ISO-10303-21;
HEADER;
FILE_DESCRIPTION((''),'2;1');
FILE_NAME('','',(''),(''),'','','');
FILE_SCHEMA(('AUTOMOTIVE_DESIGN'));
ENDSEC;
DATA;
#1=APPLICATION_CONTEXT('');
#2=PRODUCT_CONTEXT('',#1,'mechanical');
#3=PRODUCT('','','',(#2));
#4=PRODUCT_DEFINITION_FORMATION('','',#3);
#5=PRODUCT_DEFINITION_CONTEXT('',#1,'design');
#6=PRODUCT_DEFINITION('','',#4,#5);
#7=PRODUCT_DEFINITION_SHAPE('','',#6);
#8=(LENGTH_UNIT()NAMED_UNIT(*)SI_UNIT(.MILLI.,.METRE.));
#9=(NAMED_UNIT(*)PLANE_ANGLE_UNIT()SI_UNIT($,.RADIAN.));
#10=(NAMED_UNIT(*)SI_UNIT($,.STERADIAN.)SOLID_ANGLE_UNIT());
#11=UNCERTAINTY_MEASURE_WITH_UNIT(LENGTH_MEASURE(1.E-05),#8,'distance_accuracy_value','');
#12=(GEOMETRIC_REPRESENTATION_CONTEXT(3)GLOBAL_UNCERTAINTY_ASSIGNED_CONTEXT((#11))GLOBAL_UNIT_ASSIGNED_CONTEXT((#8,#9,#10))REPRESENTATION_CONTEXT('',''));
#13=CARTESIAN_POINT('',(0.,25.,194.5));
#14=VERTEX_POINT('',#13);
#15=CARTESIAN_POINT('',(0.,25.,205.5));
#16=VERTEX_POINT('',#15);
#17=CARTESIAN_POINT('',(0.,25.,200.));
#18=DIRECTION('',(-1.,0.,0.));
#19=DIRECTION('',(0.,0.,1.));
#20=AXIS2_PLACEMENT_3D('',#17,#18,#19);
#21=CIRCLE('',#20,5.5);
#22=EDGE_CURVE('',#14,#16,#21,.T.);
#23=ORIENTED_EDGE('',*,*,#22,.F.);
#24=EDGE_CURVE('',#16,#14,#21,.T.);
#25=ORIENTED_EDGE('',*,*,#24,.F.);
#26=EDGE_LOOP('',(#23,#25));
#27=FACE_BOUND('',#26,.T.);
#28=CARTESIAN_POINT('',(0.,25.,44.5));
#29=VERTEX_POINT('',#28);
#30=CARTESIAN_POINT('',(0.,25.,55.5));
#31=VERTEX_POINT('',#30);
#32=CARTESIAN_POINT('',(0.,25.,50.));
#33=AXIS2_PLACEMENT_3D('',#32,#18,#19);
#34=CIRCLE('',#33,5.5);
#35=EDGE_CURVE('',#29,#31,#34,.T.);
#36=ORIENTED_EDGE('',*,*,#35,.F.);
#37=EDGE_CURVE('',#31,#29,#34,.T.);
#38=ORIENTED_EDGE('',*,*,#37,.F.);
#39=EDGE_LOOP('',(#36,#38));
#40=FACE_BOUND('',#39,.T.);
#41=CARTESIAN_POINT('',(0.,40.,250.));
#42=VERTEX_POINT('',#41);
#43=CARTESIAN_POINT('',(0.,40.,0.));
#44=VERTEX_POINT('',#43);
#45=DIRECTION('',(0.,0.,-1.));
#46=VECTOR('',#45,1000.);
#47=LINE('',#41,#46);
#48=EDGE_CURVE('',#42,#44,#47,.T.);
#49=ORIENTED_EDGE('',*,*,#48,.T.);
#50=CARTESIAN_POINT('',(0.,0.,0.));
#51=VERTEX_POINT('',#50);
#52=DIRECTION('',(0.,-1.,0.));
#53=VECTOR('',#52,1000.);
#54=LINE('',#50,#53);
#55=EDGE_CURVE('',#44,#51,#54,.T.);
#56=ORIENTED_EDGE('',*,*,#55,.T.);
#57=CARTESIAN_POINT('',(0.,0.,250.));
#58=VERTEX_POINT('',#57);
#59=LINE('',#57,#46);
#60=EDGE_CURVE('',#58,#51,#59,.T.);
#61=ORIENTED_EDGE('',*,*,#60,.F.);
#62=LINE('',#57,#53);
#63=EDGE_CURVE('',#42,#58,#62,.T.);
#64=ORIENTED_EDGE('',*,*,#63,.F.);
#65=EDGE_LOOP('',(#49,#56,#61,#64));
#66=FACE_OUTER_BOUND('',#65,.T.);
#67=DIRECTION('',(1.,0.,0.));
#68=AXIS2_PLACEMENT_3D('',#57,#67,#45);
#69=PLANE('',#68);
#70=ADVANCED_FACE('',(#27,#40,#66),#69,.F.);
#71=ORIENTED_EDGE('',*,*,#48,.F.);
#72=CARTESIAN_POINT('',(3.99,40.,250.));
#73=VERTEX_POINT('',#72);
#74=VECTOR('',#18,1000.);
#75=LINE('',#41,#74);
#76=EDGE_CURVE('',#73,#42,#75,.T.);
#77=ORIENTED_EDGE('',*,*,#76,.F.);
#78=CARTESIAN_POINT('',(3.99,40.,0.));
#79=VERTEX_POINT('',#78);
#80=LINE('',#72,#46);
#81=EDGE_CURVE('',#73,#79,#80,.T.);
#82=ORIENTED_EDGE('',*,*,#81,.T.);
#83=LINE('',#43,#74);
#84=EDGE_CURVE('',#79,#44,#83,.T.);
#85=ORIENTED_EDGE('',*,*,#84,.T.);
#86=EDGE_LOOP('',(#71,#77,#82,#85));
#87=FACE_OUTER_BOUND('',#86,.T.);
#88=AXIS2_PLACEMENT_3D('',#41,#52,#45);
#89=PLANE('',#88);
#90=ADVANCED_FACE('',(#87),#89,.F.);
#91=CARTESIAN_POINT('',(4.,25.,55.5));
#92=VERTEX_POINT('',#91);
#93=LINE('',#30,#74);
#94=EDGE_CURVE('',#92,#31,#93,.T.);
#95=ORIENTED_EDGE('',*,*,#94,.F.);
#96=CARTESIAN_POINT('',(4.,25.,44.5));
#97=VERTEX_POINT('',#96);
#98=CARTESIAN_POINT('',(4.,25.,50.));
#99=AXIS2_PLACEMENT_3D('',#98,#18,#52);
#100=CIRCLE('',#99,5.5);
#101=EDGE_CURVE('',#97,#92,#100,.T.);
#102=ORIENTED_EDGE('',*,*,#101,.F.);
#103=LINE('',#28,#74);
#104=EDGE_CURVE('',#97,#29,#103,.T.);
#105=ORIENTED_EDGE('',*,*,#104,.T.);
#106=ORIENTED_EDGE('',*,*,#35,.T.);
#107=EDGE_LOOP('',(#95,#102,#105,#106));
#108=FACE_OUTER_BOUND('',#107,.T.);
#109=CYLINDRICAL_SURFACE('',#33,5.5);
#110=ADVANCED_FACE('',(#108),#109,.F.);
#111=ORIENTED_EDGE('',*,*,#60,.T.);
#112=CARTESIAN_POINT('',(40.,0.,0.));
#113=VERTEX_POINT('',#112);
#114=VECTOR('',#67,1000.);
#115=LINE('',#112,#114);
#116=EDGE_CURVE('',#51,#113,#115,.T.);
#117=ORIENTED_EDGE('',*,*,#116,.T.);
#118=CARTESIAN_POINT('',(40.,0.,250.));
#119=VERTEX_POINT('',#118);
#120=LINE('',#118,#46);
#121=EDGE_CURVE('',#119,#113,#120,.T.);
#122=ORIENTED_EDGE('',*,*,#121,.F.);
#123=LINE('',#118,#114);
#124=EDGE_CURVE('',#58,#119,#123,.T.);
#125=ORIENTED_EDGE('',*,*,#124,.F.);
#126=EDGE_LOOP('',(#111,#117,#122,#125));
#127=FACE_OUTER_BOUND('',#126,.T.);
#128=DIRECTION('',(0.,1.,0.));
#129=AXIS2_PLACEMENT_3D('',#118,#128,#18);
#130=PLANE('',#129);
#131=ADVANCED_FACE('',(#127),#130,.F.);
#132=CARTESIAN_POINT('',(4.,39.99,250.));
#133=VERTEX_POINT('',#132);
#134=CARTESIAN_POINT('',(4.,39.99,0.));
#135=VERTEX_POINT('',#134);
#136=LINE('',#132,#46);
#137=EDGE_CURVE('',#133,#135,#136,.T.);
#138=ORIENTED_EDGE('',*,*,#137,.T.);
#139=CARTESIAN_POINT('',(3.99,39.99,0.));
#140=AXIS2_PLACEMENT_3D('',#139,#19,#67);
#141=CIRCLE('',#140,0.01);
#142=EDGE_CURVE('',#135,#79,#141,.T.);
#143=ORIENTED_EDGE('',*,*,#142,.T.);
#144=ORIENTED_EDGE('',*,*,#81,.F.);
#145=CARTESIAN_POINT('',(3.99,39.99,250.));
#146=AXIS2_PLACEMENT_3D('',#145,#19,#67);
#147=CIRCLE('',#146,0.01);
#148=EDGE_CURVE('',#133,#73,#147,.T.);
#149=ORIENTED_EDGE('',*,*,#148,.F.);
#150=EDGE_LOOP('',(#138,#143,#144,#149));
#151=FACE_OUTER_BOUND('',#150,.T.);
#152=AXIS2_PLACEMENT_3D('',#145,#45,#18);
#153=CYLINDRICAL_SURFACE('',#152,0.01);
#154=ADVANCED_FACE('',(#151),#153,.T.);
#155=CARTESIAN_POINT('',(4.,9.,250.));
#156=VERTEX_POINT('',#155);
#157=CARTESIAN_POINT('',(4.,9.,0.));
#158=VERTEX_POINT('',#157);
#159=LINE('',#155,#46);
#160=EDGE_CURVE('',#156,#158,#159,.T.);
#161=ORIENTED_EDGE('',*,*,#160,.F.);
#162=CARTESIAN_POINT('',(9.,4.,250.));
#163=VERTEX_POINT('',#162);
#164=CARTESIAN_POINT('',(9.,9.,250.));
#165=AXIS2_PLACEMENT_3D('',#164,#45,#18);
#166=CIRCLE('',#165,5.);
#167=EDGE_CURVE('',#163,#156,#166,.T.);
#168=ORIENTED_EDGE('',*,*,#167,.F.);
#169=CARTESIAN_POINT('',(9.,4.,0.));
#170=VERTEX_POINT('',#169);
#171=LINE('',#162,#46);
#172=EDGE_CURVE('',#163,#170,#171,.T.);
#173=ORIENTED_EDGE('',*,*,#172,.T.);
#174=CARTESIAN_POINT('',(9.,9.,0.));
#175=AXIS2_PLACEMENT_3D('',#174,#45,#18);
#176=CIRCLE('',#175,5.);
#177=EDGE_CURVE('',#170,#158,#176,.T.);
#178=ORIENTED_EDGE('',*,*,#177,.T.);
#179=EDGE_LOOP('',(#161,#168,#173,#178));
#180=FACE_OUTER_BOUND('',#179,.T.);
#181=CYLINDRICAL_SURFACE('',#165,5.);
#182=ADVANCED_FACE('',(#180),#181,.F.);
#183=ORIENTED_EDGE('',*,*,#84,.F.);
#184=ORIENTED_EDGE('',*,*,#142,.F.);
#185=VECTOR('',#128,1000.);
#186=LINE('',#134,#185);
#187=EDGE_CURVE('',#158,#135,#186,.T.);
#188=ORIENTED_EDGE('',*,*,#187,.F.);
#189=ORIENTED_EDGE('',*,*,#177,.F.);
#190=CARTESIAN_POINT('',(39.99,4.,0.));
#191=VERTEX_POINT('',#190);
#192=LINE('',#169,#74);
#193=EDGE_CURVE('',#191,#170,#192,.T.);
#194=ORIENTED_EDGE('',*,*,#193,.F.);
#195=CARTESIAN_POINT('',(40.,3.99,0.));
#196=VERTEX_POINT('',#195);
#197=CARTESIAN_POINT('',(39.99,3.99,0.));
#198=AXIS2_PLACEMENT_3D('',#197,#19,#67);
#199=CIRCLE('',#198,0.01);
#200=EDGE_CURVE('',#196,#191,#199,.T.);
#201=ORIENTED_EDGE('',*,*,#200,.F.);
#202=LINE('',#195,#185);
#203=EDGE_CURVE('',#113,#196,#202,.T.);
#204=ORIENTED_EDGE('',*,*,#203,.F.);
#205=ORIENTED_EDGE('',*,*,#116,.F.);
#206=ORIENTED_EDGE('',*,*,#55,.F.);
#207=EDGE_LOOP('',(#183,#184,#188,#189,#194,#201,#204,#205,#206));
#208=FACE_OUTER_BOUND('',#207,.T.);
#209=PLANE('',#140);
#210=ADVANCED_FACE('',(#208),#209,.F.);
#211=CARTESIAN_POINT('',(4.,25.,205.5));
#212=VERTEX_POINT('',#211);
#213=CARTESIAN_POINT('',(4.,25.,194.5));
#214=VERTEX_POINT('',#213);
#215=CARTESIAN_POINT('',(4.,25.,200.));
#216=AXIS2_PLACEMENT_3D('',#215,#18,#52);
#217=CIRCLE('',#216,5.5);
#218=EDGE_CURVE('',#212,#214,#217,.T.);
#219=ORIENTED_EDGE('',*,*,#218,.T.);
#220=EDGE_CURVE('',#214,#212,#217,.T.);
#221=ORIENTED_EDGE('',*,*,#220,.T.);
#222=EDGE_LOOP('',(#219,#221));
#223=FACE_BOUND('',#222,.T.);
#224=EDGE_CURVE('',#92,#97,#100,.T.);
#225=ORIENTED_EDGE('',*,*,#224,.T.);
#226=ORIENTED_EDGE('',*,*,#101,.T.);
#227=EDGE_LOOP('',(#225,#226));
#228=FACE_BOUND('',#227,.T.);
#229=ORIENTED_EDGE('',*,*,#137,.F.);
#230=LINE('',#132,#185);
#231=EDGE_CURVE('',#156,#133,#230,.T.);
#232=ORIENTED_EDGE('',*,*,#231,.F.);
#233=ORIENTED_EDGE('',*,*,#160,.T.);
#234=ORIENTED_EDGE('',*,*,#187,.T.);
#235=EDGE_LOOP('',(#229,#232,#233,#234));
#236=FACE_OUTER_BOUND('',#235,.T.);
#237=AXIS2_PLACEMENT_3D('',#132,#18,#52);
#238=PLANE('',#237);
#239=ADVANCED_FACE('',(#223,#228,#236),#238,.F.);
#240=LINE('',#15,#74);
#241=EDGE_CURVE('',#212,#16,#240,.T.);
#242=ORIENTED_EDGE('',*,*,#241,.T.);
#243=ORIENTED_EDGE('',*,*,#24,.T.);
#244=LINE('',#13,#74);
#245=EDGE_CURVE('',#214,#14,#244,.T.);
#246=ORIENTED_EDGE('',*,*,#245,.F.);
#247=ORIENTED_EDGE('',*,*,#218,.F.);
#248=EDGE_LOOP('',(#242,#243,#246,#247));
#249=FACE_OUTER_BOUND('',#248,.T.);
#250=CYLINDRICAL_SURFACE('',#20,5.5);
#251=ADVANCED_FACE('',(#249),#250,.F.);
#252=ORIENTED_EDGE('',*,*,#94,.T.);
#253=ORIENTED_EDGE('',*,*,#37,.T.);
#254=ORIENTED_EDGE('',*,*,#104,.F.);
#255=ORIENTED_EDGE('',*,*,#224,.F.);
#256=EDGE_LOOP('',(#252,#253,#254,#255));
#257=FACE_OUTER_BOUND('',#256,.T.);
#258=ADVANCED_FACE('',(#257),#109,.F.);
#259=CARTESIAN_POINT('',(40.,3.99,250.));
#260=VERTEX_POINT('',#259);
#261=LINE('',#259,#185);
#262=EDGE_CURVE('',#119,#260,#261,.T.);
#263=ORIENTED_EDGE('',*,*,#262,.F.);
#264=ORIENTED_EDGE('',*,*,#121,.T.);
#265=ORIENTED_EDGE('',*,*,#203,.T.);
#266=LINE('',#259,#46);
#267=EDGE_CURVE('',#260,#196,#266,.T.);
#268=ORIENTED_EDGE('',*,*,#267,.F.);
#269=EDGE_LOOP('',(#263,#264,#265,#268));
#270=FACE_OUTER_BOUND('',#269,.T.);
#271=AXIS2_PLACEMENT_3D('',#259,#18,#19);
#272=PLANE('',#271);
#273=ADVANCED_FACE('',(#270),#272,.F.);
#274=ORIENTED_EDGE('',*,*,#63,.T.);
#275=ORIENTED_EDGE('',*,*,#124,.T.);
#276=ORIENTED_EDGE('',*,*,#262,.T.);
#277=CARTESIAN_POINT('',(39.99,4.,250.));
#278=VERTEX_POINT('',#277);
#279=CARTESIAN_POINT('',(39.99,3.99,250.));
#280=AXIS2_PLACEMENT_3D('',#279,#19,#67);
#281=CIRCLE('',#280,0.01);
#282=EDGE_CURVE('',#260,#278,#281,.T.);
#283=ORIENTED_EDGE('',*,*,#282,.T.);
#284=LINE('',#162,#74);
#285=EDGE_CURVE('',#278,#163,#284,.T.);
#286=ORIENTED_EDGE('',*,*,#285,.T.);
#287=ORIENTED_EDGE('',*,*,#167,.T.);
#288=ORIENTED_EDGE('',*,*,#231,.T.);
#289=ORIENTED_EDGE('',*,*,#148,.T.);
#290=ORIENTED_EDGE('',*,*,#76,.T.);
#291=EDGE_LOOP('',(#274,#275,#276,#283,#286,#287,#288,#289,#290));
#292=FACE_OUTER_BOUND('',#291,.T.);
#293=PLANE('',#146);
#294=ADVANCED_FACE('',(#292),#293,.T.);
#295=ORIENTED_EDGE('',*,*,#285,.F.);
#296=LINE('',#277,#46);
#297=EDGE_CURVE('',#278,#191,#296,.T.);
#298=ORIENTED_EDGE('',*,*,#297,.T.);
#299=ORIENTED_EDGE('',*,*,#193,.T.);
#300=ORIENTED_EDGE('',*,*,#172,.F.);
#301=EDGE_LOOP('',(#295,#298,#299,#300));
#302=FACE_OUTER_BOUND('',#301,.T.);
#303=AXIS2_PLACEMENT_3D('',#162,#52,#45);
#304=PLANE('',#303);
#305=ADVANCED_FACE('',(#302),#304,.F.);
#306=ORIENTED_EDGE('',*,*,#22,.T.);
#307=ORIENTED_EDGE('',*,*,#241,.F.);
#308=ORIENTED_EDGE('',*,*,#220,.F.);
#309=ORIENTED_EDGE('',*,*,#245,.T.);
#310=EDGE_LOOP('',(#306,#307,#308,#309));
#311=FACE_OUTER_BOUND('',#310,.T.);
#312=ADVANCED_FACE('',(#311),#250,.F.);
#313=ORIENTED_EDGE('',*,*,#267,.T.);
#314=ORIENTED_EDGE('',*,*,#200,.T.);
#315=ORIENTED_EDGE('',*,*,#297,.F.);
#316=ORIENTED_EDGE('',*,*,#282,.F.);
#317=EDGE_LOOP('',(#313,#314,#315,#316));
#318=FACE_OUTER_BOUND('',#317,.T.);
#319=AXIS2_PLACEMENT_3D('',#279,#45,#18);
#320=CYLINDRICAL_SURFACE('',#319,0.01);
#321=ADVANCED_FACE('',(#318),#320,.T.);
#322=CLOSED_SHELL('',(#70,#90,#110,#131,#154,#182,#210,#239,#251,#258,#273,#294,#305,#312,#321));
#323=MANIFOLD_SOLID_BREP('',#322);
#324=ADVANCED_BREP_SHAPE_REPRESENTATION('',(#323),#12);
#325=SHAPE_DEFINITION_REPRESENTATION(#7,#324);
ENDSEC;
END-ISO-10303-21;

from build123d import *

# Parameters (mm, degrees)
EXTRUDE_1_DEPTH             = 250
HOLE_WIZARD_11_0_11_1_D     = 11
HOLE_WIZARD_11_0_11_1_DEPTH = 10
HOLE_WIZARD_11_0_11_1_TIP   = 3.304733405


with BuildPart() as part:
    # 草图1 → 拉伸1 (new body)
    with BuildSketch(Plane.XY):
        with BuildLine():
            Line((0, 0), (0, 40))
            Line((0, 40), (3.99, 40))
            ThreePointArc((3.99, 40), (3.997071068, 39.997071068), (4, 39.99))
            Line((4, 39.99), (4, 9))
            ThreePointArc((4, 9), (5.464466094, 5.464466094), (9, 4))
            Line((9, 4), (39.99, 4))
            ThreePointArc((39.99, 4), (39.997071068, 3.997071068), (40, 3.99))
            Line((40, 3.99), (40, 0))
            Line((40, 0), (0, 0))
        make_face()
    extrude(amount=EXTRUDE_1_DEPTH)

    # Ø11.0 (11) 直径孔1
    with Locations(Plane.ZY):
        with Locations((200, 25), (50, 25)):
            Hole(HOLE_WIZARD_11_0_11_1_D / 2, depth=HOLE_WIZARD_11_0_11_1_DEPTH)
            with Locations((0, 0, -(HOLE_WIZARD_11_0_11_1_DEPTH + HOLE_WIZARD_11_0_11_1_TIP / 2))):  # 118° drill point
                Cone(0, HOLE_WIZARD_11_0_11_1_D / 2, HOLE_WIZARD_11_0_11_1_TIP, mode=Mode.SUBTRACT)


solid = part.part
